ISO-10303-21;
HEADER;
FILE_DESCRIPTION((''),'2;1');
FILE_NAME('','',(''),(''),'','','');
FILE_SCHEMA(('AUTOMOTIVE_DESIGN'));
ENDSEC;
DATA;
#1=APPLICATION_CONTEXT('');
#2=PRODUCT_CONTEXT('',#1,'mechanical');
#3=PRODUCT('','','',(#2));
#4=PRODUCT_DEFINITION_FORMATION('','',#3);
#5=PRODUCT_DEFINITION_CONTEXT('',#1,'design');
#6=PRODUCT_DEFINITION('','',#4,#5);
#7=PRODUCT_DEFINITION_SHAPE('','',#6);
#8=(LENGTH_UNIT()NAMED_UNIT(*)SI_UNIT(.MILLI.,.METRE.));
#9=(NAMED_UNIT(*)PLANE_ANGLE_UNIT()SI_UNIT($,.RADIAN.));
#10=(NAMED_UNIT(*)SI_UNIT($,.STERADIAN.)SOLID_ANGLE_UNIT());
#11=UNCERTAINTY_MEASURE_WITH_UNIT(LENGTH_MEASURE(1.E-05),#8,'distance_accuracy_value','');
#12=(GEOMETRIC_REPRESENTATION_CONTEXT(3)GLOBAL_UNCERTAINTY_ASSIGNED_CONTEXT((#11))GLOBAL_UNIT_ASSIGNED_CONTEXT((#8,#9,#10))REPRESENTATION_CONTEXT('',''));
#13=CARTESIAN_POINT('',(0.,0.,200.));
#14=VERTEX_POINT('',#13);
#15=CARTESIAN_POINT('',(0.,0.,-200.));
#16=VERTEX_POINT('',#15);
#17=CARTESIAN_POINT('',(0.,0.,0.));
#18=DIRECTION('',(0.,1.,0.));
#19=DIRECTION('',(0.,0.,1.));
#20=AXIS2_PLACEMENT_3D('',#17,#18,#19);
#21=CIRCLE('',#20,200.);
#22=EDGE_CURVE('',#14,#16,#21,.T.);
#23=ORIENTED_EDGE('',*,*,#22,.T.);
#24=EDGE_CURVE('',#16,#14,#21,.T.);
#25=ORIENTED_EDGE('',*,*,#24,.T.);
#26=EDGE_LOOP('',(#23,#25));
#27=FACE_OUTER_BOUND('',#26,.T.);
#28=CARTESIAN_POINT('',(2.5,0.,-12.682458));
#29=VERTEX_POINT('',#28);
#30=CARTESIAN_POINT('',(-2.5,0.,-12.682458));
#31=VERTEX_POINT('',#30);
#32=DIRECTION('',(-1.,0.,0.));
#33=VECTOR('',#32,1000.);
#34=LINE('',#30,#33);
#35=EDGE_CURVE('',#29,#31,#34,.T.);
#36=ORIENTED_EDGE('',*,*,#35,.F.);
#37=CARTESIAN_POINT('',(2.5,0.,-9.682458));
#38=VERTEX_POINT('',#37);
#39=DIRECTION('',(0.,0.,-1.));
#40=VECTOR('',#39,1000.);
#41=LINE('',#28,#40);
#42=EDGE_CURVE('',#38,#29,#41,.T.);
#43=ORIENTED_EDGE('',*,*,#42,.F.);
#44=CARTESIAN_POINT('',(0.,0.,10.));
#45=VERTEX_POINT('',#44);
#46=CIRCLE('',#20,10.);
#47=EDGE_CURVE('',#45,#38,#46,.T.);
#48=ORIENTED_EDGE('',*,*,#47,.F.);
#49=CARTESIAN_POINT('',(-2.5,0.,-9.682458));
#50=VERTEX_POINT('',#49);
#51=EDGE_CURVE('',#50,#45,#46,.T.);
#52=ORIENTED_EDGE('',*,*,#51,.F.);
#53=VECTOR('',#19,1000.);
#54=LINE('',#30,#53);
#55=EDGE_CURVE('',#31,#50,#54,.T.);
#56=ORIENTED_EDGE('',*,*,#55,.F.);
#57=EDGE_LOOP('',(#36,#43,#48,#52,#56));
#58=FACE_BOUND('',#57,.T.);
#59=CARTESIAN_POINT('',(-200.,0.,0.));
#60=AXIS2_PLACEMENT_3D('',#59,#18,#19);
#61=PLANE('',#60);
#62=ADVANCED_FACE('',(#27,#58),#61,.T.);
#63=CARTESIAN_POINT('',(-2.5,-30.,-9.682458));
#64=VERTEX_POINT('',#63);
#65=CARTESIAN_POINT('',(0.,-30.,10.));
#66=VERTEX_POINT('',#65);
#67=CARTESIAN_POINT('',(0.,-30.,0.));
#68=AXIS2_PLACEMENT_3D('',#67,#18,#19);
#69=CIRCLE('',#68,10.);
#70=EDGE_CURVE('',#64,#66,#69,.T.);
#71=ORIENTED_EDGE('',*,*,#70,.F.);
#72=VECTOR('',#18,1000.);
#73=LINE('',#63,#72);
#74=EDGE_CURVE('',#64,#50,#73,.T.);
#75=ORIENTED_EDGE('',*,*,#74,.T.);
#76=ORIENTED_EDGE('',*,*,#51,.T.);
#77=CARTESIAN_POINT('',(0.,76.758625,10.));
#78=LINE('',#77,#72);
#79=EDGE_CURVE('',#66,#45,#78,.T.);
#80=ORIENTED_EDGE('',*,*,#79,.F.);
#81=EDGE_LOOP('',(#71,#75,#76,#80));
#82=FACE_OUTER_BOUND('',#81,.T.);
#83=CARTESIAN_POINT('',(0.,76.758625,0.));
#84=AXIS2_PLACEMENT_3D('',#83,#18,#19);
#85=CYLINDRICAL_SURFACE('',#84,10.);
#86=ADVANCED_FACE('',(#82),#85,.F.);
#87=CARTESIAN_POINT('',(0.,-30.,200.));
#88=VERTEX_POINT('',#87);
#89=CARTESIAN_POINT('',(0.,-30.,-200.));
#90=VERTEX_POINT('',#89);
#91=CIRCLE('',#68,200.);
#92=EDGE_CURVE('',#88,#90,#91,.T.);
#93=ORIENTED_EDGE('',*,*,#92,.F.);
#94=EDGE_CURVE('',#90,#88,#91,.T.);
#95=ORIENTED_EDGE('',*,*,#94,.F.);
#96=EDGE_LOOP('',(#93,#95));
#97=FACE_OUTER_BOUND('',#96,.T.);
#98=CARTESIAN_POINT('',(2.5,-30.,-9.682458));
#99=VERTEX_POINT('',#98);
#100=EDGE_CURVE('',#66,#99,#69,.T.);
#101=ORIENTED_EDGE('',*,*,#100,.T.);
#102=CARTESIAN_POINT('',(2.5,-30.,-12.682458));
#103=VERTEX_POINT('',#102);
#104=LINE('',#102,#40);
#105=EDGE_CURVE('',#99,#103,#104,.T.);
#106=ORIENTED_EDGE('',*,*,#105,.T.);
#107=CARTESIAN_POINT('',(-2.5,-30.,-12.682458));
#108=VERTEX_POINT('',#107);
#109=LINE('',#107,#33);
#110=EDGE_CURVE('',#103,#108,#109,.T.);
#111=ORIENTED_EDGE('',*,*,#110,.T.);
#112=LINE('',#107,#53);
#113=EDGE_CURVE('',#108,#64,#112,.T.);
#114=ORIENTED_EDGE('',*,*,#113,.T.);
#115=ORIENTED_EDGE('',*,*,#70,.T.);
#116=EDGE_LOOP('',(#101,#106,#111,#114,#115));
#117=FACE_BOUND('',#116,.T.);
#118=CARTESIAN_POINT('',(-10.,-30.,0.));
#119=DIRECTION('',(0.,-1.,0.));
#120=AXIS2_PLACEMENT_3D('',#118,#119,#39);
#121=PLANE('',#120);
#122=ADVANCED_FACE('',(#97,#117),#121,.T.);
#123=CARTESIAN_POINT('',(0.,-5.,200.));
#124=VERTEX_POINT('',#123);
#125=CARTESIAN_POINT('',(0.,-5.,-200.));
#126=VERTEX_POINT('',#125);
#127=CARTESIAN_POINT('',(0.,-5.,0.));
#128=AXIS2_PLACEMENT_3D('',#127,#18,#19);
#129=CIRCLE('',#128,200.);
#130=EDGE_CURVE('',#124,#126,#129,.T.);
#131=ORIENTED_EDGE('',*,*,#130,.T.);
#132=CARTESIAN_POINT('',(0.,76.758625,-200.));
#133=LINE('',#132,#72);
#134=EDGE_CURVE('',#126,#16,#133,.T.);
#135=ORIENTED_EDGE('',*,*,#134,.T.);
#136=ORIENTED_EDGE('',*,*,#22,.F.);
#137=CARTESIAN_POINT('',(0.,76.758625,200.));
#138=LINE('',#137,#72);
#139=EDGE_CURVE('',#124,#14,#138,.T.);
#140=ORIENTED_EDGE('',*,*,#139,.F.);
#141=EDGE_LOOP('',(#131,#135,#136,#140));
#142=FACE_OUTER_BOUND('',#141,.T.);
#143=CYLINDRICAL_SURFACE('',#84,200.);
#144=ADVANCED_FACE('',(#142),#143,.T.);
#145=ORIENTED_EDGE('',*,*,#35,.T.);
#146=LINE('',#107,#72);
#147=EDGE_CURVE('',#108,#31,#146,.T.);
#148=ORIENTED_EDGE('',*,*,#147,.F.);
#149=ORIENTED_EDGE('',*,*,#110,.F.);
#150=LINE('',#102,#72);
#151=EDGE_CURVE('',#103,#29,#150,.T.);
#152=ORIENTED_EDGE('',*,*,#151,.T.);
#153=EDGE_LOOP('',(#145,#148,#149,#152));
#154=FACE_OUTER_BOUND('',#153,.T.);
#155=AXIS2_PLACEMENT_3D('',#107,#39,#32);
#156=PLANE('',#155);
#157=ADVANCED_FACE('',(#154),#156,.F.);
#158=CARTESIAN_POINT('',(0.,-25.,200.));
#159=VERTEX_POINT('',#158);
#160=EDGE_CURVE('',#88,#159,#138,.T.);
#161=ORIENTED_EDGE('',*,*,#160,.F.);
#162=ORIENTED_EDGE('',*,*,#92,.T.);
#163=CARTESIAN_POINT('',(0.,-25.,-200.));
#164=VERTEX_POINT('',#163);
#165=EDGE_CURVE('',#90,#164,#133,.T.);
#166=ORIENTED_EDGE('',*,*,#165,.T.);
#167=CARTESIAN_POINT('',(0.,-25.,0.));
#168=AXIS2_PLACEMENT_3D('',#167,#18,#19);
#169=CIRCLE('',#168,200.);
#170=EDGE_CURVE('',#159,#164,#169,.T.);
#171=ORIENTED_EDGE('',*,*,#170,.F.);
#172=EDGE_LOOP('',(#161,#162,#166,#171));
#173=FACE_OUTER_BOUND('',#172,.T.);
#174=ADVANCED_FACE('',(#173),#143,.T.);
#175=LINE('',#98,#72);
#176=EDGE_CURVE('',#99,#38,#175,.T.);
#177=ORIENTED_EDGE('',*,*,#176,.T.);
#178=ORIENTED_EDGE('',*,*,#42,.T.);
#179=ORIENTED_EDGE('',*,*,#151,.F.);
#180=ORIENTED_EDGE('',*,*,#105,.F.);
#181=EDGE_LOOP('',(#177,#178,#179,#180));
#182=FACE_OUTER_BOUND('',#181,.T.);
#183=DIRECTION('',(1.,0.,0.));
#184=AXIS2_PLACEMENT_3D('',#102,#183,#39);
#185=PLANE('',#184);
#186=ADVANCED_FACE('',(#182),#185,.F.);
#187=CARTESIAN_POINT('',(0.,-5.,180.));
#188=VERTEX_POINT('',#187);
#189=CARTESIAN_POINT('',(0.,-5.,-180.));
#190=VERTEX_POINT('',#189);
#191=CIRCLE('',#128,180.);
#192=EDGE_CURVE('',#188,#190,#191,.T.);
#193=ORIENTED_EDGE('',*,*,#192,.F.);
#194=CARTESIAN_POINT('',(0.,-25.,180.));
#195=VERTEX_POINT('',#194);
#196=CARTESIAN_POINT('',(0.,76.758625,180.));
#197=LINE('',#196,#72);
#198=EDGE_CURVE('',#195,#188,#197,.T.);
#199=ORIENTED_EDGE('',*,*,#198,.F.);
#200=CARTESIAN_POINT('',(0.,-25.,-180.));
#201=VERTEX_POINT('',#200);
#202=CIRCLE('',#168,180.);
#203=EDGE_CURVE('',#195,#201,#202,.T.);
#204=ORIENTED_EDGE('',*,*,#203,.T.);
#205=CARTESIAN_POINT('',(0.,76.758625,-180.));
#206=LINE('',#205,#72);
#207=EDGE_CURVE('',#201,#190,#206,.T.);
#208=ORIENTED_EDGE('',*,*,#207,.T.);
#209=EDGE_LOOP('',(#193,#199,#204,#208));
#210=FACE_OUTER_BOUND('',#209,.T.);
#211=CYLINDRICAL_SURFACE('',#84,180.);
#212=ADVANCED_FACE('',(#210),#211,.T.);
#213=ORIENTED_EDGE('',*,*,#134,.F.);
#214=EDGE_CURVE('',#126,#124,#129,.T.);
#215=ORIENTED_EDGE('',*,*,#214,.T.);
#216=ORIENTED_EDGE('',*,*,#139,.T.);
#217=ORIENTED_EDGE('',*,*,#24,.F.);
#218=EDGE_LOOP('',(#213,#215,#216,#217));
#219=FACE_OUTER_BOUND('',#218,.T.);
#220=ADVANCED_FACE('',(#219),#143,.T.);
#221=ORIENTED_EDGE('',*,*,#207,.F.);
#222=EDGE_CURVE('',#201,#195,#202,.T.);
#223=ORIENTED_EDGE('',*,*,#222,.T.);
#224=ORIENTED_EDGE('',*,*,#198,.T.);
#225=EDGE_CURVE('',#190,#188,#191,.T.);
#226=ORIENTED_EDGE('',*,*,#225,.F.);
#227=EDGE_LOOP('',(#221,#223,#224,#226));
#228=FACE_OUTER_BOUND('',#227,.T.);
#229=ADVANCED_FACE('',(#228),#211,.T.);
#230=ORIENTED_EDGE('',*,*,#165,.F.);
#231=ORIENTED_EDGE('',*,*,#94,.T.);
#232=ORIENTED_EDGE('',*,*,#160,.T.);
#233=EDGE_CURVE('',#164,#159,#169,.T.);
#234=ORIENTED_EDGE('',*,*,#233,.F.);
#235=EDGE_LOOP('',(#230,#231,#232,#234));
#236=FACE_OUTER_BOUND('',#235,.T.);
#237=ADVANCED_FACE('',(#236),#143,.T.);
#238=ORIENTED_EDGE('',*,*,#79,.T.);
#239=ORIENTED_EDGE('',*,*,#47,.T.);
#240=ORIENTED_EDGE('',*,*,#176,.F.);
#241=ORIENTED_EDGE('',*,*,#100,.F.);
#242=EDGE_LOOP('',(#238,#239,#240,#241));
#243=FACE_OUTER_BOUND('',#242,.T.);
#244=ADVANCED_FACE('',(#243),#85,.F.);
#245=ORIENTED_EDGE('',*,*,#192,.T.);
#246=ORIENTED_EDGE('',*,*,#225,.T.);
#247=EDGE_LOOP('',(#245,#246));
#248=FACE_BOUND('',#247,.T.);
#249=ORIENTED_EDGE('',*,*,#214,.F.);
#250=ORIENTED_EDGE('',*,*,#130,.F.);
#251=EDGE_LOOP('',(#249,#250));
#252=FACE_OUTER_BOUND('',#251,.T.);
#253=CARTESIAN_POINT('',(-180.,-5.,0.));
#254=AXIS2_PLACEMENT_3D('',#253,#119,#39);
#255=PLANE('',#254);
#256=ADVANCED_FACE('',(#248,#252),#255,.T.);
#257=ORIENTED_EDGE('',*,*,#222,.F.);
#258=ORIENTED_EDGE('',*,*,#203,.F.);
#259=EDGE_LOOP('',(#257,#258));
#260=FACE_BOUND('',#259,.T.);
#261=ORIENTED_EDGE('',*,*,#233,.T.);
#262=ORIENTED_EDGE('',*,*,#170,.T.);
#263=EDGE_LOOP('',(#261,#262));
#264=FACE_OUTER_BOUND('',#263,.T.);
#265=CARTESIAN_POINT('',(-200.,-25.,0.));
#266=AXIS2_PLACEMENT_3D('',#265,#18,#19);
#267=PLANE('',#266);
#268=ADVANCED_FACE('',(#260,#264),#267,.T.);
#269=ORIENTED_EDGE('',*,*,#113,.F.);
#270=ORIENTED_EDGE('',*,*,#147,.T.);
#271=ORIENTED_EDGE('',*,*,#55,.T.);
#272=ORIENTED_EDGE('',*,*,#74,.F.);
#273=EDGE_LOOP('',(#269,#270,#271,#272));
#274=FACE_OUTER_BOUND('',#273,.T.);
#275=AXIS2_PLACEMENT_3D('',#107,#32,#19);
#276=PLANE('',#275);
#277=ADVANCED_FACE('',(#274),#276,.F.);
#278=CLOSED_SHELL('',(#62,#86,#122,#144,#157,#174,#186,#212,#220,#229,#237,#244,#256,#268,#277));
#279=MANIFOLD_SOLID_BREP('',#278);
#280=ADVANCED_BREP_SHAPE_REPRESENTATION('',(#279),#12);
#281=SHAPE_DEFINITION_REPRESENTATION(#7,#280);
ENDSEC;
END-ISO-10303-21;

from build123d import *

# Parameters (mm, degrees)
CUT_EXTRUDE1_DEPTH = 285.429253067


with BuildPart() as part:
    # Sketch1 → Revolve1 (revolve)
    with BuildSketch(Plane.XY, mode=Mode.PRIVATE) as revolve1_sk:
        Polygon((-10, 0), (-10, -30), (-200, -30), (-200, -25), (-180, -25), (-180, -5), (-200, -5), (-200, 0), align=None)
    revolve(revolve1_sk.sketch.rotate(Axis((0, 76.758624558, 0), (0, -1, 0)), 270), axis=Axis((0, 76.758624558, 0), (0, -1, 0)))

    # Sketch2 → Cut-Extrude1 (cut, through all)
    with BuildSketch(Plane(origin=(0, 0, 0), x_dir=(1, 0, 0), z_dir=(0, 1, 0))):
        with BuildLine():
            Line((-2.5, 12.682458366), (-2.5, 9.682458366))
            ThreePointArc((-2.5, 9.682458366), (0, 10), (2.5, 9.682458366))
            Line((2.5, 9.682458366), (2.5, 12.682458366))
            Line((2.5, 12.682458366), (-2.5, 12.682458366))
        make_face()
    extrude(amount=-CUT_EXTRUDE1_DEPTH, mode=Mode.SUBTRACT)


solid = part.part
